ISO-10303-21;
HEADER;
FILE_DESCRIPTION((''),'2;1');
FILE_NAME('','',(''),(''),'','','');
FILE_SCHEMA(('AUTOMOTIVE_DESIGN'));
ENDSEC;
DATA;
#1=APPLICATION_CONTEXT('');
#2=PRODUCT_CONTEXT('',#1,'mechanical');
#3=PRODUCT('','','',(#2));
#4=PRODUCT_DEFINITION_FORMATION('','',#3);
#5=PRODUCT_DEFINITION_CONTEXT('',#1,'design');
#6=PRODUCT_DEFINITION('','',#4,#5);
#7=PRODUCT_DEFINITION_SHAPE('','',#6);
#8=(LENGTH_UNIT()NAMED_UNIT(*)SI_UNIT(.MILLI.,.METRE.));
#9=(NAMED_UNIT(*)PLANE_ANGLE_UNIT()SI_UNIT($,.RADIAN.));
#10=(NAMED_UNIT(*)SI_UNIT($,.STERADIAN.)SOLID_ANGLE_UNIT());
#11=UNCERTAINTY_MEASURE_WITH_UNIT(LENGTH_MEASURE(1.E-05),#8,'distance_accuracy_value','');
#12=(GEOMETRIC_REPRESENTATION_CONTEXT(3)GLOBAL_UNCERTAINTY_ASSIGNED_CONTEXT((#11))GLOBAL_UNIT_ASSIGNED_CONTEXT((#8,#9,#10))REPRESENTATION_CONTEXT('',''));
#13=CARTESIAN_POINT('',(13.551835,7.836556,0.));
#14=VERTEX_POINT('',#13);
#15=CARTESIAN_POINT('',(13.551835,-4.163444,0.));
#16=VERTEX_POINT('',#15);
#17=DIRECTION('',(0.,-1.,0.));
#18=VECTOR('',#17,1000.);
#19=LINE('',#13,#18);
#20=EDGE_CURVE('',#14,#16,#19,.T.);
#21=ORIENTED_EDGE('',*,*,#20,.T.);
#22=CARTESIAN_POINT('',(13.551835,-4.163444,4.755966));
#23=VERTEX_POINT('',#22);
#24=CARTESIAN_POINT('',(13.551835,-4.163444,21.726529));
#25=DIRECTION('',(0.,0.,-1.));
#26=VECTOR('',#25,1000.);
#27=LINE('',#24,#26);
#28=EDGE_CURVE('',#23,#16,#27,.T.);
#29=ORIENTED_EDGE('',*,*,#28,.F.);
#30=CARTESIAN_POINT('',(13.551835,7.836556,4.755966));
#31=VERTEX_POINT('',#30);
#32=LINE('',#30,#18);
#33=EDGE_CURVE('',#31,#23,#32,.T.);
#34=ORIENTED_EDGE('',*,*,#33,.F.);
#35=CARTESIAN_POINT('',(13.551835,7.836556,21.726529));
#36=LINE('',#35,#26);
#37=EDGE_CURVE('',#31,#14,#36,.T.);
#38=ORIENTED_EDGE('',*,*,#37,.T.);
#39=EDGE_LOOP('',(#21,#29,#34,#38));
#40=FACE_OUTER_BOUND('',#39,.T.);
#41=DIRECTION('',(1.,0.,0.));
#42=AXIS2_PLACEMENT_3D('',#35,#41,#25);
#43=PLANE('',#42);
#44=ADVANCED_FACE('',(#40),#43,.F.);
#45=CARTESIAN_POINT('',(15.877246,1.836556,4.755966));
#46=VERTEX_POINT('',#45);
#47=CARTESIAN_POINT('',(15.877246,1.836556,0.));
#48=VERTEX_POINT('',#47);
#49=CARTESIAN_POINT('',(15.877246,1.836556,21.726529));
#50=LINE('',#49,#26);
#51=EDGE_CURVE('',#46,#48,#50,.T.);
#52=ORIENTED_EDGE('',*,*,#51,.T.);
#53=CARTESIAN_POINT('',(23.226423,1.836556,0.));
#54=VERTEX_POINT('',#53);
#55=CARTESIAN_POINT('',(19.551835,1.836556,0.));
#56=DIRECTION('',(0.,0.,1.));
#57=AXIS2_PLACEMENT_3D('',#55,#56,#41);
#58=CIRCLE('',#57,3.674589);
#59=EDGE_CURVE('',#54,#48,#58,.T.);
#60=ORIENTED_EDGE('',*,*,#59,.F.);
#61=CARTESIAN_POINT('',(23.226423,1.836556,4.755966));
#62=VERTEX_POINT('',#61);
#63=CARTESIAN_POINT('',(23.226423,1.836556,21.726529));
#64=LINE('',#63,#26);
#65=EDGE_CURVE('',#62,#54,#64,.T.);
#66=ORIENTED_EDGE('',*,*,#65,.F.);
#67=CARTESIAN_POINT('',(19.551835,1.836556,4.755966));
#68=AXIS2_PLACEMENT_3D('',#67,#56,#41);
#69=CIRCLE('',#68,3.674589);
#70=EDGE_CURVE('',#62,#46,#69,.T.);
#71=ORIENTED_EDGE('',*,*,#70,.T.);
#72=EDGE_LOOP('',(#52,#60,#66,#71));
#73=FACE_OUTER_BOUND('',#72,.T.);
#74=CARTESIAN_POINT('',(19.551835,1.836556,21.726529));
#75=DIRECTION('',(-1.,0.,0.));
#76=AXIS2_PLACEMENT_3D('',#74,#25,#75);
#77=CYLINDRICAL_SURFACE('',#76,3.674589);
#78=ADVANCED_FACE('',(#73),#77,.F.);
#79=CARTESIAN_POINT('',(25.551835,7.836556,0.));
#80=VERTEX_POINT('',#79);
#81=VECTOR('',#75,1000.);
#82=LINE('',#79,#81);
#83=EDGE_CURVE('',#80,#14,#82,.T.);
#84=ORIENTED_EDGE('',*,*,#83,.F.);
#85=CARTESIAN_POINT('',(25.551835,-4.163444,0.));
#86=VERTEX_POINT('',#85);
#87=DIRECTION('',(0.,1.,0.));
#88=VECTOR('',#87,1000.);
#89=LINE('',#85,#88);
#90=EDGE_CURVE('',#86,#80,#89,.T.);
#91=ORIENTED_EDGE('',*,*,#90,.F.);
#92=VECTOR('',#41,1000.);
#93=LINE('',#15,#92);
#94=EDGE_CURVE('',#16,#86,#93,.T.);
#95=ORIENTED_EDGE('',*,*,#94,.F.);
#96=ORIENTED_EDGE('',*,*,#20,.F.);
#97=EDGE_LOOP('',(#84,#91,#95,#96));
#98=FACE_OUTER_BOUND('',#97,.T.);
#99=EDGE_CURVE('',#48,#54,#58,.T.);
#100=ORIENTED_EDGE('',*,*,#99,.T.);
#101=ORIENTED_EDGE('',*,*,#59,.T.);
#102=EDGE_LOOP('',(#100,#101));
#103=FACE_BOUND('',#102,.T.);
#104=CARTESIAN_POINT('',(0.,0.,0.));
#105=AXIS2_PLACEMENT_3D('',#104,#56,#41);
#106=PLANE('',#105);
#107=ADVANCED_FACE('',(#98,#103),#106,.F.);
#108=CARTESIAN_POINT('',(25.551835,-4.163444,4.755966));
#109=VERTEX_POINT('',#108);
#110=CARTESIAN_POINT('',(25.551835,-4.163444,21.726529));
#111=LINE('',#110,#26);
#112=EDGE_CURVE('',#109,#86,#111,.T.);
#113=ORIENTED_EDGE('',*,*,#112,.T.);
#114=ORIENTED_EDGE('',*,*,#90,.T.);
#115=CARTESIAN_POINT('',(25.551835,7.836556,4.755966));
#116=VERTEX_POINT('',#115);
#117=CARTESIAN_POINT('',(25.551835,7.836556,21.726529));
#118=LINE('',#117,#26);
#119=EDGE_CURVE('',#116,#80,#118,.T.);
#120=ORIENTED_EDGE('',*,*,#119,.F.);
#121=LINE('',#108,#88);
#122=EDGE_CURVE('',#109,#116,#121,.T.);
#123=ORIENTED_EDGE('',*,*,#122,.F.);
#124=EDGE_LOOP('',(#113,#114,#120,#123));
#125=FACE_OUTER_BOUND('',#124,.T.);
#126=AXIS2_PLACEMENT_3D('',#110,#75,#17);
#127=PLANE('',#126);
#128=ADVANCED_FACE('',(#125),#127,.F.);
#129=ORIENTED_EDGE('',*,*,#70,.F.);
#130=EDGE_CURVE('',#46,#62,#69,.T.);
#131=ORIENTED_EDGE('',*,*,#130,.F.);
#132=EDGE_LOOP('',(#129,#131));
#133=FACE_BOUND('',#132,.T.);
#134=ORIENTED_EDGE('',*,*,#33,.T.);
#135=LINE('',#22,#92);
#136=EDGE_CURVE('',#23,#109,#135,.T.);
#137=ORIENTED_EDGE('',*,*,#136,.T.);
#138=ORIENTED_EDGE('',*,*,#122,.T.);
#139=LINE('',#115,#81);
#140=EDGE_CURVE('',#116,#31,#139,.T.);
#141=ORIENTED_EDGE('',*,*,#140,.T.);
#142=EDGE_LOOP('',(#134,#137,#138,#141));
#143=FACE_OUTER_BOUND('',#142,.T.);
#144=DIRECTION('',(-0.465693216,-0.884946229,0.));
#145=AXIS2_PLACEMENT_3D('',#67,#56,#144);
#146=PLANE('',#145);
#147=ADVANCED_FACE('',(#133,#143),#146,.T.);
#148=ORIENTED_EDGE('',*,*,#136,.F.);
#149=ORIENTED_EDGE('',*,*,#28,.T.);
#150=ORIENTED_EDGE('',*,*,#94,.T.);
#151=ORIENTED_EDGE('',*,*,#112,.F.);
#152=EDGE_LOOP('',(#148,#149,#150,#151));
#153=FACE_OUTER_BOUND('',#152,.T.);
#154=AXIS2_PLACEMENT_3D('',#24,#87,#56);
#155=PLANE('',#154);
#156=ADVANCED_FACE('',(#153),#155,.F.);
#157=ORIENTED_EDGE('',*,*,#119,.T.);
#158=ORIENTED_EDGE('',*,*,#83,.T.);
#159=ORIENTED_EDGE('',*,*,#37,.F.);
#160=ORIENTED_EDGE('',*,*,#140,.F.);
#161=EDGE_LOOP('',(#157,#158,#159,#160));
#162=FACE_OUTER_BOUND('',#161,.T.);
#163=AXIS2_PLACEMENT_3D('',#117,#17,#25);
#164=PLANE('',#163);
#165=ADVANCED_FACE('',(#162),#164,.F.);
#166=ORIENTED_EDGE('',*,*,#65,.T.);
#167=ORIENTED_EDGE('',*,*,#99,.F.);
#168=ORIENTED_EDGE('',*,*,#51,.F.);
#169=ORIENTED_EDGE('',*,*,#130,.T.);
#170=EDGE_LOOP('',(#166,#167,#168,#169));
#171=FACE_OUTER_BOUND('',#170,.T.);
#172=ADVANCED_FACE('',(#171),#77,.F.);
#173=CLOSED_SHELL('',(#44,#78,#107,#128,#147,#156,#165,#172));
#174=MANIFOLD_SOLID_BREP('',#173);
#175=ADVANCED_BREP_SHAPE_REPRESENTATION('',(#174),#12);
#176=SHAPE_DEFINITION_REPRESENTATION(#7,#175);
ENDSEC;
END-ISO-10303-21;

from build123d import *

# Parameters (mm, degrees)
SKETCH1_W           = 12
SKETCH1_H           = 12
SKETCH1_R           = 3.674588618
BOSS_EXTRUDE1_DEPTH = 4.755965796


with BuildPart() as part:
    # Sketch1 → Boss-Extrude1 (new body)
    with BuildSketch(Plane.XY):
        with Locations((19.551834603, 1.836555855)):
            Rectangle(SKETCH1_W, SKETCH1_H)
        with Locations((19.551834603, 1.836555855)):
            Circle(SKETCH1_R, mode=Mode.SUBTRACT)
    extrude(amount=BOSS_EXTRUDE1_DEPTH)


solid = part.part
